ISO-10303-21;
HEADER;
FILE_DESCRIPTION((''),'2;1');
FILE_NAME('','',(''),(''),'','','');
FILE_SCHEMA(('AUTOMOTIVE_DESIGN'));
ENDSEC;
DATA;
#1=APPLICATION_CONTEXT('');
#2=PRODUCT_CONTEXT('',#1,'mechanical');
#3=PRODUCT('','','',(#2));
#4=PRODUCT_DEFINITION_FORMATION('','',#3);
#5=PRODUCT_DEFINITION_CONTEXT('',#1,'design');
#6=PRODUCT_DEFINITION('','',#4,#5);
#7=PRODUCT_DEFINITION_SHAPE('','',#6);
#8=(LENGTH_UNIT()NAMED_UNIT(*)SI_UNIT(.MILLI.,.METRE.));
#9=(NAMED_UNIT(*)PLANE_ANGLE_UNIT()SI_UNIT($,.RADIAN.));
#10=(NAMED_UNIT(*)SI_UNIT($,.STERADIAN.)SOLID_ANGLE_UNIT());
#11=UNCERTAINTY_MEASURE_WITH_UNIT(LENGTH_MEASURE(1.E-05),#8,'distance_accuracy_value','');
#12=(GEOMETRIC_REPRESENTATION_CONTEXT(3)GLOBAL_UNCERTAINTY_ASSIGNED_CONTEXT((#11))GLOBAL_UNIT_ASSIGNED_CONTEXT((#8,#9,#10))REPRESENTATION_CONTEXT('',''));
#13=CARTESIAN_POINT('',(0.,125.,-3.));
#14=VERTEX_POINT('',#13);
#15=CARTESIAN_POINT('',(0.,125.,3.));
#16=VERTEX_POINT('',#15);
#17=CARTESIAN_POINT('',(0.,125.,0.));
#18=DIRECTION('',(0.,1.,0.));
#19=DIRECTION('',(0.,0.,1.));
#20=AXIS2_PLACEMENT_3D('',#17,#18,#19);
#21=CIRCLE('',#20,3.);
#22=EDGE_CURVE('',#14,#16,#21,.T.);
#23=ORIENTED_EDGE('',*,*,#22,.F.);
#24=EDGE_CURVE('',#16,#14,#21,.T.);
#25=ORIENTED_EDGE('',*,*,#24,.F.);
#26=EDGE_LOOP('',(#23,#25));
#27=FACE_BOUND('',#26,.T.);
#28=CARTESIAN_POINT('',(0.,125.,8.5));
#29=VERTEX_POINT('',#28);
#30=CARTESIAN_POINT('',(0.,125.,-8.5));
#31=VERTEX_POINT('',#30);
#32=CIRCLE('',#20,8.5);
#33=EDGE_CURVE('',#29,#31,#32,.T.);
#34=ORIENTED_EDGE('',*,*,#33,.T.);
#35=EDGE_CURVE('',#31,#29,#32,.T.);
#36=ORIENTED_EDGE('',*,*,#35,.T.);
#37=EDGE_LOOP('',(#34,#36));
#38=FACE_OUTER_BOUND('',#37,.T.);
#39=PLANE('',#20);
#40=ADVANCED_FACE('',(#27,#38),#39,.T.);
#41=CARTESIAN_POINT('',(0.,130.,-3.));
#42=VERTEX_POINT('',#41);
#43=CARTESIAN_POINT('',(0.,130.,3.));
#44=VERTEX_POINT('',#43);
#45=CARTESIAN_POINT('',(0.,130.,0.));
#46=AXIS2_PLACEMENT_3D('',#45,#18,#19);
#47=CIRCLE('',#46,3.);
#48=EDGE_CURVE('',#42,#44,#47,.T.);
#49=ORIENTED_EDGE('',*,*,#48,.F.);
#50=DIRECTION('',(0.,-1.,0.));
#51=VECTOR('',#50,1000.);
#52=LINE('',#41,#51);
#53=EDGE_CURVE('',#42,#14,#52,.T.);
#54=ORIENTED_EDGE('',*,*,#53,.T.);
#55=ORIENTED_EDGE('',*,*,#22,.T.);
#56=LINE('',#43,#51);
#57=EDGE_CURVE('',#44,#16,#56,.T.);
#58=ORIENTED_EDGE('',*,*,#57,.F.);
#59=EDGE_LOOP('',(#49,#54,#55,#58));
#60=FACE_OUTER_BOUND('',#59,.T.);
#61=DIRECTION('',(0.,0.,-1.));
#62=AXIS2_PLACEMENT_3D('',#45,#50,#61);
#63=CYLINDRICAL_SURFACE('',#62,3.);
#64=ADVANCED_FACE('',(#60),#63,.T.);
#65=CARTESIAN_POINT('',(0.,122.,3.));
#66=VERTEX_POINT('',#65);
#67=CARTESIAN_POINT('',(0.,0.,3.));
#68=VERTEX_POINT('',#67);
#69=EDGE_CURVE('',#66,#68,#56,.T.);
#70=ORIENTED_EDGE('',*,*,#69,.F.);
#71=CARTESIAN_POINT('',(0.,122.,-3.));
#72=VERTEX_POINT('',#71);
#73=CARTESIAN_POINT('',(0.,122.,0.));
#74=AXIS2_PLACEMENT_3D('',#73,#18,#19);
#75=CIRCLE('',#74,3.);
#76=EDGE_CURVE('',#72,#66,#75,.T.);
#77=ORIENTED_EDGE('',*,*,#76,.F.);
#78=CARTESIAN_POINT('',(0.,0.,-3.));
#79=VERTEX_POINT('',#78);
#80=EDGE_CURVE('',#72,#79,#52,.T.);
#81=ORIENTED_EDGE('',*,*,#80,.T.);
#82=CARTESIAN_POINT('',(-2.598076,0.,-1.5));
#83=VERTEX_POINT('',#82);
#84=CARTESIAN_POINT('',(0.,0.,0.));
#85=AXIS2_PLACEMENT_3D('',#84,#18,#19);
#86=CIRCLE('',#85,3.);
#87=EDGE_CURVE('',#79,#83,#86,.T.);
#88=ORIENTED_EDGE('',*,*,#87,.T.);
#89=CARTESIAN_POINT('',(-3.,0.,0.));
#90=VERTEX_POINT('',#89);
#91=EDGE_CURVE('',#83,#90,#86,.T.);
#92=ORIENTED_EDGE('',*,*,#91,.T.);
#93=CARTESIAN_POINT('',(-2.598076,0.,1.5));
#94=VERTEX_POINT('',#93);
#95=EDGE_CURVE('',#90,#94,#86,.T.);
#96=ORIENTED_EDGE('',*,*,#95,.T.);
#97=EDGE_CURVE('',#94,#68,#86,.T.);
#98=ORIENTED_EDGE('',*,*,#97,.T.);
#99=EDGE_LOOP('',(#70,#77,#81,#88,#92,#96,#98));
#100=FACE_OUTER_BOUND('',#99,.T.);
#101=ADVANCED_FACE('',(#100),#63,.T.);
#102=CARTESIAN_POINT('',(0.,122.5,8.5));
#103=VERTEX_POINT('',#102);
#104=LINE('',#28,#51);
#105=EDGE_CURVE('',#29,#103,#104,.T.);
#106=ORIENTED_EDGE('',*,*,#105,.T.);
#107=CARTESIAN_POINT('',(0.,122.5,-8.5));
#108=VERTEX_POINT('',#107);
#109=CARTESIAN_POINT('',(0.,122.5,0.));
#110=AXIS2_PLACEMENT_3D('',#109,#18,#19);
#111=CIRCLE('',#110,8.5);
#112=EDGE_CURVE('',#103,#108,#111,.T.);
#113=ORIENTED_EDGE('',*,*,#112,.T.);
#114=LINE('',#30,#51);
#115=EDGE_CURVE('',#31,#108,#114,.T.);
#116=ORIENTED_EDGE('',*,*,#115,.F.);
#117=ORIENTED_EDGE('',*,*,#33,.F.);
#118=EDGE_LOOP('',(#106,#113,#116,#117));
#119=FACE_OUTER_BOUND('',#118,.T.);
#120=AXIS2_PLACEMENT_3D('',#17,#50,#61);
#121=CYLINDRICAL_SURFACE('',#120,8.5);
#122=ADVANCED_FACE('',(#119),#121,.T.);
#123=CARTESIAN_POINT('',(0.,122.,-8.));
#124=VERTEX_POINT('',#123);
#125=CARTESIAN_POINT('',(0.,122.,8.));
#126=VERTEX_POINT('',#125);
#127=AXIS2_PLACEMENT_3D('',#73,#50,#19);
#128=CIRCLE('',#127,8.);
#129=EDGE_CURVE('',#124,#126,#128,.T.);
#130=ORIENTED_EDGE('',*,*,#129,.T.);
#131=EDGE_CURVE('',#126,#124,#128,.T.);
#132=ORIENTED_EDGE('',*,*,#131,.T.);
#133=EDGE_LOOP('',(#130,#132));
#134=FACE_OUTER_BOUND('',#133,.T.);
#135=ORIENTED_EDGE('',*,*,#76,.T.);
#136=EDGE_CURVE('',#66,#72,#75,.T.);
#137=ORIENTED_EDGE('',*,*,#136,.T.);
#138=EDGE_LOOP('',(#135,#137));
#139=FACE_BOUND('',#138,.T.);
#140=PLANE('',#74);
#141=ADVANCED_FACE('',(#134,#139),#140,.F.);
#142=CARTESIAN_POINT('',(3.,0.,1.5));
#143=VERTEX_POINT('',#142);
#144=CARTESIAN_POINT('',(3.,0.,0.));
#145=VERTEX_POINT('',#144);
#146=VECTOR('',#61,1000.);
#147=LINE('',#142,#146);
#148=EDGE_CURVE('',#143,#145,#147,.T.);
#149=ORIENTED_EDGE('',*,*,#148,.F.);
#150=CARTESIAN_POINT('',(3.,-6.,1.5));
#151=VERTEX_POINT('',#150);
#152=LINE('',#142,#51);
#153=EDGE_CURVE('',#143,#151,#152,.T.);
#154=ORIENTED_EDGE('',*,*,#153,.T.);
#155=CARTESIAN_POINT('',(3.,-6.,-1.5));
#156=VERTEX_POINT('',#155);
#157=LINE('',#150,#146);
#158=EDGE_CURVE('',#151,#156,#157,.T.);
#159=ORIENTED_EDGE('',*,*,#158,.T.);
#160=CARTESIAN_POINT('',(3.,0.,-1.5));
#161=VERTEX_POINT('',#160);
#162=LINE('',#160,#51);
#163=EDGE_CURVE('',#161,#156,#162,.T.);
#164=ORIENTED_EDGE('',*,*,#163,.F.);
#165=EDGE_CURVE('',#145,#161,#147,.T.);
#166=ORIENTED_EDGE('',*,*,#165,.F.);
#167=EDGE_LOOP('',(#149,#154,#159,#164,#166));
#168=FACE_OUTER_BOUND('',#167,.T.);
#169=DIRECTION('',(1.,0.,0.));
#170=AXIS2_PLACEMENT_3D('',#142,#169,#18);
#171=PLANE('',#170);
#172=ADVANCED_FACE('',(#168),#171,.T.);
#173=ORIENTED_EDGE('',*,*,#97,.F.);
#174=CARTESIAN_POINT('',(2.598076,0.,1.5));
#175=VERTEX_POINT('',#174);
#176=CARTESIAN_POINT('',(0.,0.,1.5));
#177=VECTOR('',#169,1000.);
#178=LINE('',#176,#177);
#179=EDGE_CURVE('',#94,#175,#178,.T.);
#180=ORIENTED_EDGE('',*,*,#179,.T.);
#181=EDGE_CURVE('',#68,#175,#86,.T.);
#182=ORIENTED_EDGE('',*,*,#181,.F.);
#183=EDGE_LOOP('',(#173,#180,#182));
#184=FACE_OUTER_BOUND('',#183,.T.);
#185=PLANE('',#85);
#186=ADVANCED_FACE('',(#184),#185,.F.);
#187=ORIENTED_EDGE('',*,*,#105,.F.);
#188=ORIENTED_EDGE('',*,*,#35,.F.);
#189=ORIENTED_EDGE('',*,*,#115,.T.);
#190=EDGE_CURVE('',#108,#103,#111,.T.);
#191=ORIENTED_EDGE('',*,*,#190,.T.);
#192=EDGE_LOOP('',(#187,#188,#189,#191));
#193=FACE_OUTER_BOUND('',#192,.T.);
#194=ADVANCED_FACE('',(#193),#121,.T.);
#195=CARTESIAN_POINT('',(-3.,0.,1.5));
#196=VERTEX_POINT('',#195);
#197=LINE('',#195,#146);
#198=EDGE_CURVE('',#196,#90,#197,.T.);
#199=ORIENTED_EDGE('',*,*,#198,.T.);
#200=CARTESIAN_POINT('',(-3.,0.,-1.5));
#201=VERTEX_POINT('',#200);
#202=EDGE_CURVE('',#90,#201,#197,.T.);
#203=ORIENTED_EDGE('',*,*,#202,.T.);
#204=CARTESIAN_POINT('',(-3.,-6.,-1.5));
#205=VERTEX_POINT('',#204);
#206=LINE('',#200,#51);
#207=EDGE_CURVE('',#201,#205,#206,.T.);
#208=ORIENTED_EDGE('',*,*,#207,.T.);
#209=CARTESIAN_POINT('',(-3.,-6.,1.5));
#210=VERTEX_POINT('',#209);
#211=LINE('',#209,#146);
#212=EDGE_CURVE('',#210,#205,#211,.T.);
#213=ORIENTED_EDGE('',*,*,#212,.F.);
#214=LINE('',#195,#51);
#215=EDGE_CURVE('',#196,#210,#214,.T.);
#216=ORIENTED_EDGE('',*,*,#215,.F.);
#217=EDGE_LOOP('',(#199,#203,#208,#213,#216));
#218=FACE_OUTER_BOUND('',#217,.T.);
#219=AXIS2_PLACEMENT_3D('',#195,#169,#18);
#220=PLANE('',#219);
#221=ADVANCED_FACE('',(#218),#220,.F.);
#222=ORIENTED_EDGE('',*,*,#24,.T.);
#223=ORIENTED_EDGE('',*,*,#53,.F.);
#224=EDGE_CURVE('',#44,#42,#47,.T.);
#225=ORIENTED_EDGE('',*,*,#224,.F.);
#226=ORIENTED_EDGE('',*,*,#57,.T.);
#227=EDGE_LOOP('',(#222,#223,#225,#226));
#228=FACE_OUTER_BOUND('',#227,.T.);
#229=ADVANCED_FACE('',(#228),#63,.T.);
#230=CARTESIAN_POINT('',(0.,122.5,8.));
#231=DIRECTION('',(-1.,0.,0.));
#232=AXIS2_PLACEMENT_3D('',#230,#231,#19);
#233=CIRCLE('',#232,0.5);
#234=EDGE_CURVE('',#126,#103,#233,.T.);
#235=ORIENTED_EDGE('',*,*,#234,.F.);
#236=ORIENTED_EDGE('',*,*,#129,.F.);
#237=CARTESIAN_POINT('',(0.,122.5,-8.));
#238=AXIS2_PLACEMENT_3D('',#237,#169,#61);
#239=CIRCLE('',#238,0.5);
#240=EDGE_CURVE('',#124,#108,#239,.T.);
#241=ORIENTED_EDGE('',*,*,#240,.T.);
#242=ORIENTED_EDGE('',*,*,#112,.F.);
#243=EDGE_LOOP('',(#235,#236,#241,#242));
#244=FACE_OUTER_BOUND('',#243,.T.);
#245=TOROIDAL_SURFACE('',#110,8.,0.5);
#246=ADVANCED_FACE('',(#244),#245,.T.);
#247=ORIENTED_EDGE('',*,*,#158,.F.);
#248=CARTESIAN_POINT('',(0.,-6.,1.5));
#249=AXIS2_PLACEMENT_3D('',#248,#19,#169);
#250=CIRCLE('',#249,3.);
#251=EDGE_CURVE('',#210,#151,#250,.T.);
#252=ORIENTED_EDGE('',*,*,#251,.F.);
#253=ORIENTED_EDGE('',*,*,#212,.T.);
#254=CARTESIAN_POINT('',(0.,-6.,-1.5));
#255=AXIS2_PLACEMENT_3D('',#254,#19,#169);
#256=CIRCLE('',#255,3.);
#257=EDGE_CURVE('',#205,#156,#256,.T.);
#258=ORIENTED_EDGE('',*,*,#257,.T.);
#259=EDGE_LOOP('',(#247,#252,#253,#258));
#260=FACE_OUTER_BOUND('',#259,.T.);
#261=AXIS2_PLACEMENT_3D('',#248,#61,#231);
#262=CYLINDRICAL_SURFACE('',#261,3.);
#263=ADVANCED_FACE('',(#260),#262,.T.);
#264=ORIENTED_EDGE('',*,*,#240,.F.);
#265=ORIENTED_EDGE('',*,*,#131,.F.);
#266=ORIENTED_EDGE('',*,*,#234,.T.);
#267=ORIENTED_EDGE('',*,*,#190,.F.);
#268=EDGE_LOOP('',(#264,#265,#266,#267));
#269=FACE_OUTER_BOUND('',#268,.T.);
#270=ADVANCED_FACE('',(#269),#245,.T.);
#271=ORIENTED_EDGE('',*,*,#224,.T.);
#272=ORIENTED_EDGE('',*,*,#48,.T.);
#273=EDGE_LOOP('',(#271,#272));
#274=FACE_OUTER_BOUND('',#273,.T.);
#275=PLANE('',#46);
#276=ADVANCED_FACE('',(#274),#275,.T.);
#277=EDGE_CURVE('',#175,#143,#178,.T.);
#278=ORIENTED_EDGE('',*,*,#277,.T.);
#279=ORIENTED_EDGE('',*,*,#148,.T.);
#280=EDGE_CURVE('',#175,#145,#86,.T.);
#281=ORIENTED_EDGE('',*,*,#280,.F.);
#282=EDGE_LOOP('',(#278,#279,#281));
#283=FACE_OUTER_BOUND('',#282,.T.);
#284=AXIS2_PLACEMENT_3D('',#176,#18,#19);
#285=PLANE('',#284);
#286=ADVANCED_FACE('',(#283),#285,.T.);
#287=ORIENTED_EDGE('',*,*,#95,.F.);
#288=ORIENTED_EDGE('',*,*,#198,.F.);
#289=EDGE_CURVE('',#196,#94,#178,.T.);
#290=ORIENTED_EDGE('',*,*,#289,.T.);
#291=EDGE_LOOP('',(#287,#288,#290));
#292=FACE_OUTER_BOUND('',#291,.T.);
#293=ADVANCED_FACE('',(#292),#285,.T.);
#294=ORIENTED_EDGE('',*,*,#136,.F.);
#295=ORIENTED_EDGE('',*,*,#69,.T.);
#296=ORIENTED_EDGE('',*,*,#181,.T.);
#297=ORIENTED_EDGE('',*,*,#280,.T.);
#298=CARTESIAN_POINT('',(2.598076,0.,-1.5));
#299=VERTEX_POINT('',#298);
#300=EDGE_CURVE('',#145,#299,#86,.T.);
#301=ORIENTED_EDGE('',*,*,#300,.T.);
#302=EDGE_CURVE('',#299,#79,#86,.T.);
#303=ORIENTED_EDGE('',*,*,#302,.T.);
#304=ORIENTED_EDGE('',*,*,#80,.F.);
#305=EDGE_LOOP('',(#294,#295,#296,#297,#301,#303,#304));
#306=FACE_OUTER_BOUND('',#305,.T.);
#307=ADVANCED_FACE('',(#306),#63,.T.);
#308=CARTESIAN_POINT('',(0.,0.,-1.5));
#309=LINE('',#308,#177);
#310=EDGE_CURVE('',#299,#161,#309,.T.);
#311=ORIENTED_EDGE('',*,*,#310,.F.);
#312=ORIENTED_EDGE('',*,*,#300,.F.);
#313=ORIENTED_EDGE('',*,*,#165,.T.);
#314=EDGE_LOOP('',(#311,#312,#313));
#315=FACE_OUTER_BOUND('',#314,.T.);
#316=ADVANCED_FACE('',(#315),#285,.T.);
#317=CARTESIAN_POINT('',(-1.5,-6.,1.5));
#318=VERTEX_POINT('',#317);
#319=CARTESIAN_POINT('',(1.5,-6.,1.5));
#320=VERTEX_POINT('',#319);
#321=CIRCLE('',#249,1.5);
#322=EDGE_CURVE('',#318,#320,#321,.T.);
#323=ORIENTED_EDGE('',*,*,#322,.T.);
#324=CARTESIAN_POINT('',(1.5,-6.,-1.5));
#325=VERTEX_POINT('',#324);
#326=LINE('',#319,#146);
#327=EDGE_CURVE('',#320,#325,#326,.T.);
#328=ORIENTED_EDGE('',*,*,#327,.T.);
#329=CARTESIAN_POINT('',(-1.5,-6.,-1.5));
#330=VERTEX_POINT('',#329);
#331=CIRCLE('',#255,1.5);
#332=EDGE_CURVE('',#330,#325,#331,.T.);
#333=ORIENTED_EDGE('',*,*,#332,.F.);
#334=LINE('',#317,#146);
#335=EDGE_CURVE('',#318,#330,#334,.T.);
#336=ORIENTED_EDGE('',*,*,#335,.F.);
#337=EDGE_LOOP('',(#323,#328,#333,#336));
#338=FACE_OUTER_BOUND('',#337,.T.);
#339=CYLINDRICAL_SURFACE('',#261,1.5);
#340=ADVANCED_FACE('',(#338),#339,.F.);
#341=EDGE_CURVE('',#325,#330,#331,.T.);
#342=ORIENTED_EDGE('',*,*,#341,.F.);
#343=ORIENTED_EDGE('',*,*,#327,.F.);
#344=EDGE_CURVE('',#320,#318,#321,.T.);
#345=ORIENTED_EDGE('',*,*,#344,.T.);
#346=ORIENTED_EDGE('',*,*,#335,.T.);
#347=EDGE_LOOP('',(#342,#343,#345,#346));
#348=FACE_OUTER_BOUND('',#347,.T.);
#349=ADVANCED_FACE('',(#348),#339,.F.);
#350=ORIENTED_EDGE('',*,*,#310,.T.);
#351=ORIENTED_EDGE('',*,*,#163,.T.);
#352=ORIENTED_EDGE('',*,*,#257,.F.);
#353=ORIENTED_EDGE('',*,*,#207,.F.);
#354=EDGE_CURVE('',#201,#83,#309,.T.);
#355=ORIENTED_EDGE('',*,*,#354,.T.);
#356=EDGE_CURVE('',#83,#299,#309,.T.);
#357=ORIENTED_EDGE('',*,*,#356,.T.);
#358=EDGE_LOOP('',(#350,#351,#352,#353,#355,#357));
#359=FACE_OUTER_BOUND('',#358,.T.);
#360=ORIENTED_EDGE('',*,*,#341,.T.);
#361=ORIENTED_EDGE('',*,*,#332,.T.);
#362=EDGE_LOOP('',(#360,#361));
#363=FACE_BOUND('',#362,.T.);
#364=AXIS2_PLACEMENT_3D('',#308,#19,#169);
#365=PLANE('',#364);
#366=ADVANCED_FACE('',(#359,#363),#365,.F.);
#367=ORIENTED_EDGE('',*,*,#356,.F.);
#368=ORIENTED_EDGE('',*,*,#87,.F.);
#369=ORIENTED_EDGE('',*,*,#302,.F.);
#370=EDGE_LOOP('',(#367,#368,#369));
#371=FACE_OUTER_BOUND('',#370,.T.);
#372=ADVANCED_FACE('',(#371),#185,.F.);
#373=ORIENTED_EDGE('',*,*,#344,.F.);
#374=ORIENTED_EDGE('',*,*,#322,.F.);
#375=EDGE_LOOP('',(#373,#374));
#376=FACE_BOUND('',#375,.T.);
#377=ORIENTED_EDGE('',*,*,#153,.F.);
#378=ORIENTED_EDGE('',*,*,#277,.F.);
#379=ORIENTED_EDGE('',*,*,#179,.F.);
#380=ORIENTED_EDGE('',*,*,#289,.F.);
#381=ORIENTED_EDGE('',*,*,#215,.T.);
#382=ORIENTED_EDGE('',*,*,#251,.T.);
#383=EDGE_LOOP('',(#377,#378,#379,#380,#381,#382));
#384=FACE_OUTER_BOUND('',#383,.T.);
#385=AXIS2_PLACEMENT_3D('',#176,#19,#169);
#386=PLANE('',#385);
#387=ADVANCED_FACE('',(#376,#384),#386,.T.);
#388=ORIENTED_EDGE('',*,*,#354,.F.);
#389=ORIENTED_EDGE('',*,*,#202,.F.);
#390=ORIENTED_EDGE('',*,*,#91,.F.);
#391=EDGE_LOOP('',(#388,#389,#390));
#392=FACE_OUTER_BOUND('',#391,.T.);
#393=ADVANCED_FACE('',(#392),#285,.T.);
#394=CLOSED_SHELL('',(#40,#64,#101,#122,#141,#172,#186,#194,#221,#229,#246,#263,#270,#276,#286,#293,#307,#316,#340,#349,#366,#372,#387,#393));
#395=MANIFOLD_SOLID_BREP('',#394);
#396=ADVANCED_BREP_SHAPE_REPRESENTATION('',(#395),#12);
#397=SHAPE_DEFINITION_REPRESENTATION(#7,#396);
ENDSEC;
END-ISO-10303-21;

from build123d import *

# Parameters (mm, degrees)
SKETCH1_R           = 3
BOSS_EXTRUDE1_DEPTH = 130
SKETCH2_R           = 3
SKETCH2_R_2         = 1.5
BOSS_EXTRUDE2_DEPTH = 1.5
SKETCH3_R           = 8.5
BOSS_EXTRUDE3_DEPTH = 3
FILLET1_R           = 0.5


with BuildPart() as part:
    # Sketch1 → Boss-Extrude1 (new body)
    with BuildSketch(Plane(origin=(0, 0, 0), x_dir=(1, 0, 0), z_dir=(0, 1, 0))):
        with Locations(Location((0, 0, 0), (0, 0, 270))):
            Circle(SKETCH1_R)
    extrude(amount=BOSS_EXTRUDE1_DEPTH)

    # Sketch2 → Boss-Extrude2 (add, symmetric)
    # profile 1 of 2: a face of its own
    with BuildSketch(Plane.XY):
        with BuildLine():
            Line((3, 0), (-3, 0))
            Line((-3, 0), (-3, -6))
            ThreePointArc((-3, -6), (0, -3), (3, -6))
            Line((3, -6), (3, 0))
        make_face()
    # profile 2 of 2: a face of its own
    with BuildSketch(Plane.XY):
        with Locations((0, -6)):
            Circle(SKETCH2_R)
        with Locations((0, -6)):
            Circle(SKETCH2_R_2, mode=Mode.SUBTRACT)
    extrude(amount=BOSS_EXTRUDE2_DEPTH, both=True)

    # Sketch3 → Boss-Extrude3 (add)
    with BuildSketch(Plane(origin=(0, 122, 0), x_dir=(1, 0, 0), z_dir=(0, 1, 0))):
        with Locations(Location((0, 0, 0), (0, 0, 270))):
            Circle(SKETCH3_R)
    extrude(amount=BOSS_EXTRUDE3_DEPTH)

    # Fillet1
    fillet1_edges = [part.edges().sort_by_distance(p)[0] for p in [
        (0, 122, -8.5),
    ]]
    fillet(fillet1_edges, radius=FILLET1_R)


solid = part.part
